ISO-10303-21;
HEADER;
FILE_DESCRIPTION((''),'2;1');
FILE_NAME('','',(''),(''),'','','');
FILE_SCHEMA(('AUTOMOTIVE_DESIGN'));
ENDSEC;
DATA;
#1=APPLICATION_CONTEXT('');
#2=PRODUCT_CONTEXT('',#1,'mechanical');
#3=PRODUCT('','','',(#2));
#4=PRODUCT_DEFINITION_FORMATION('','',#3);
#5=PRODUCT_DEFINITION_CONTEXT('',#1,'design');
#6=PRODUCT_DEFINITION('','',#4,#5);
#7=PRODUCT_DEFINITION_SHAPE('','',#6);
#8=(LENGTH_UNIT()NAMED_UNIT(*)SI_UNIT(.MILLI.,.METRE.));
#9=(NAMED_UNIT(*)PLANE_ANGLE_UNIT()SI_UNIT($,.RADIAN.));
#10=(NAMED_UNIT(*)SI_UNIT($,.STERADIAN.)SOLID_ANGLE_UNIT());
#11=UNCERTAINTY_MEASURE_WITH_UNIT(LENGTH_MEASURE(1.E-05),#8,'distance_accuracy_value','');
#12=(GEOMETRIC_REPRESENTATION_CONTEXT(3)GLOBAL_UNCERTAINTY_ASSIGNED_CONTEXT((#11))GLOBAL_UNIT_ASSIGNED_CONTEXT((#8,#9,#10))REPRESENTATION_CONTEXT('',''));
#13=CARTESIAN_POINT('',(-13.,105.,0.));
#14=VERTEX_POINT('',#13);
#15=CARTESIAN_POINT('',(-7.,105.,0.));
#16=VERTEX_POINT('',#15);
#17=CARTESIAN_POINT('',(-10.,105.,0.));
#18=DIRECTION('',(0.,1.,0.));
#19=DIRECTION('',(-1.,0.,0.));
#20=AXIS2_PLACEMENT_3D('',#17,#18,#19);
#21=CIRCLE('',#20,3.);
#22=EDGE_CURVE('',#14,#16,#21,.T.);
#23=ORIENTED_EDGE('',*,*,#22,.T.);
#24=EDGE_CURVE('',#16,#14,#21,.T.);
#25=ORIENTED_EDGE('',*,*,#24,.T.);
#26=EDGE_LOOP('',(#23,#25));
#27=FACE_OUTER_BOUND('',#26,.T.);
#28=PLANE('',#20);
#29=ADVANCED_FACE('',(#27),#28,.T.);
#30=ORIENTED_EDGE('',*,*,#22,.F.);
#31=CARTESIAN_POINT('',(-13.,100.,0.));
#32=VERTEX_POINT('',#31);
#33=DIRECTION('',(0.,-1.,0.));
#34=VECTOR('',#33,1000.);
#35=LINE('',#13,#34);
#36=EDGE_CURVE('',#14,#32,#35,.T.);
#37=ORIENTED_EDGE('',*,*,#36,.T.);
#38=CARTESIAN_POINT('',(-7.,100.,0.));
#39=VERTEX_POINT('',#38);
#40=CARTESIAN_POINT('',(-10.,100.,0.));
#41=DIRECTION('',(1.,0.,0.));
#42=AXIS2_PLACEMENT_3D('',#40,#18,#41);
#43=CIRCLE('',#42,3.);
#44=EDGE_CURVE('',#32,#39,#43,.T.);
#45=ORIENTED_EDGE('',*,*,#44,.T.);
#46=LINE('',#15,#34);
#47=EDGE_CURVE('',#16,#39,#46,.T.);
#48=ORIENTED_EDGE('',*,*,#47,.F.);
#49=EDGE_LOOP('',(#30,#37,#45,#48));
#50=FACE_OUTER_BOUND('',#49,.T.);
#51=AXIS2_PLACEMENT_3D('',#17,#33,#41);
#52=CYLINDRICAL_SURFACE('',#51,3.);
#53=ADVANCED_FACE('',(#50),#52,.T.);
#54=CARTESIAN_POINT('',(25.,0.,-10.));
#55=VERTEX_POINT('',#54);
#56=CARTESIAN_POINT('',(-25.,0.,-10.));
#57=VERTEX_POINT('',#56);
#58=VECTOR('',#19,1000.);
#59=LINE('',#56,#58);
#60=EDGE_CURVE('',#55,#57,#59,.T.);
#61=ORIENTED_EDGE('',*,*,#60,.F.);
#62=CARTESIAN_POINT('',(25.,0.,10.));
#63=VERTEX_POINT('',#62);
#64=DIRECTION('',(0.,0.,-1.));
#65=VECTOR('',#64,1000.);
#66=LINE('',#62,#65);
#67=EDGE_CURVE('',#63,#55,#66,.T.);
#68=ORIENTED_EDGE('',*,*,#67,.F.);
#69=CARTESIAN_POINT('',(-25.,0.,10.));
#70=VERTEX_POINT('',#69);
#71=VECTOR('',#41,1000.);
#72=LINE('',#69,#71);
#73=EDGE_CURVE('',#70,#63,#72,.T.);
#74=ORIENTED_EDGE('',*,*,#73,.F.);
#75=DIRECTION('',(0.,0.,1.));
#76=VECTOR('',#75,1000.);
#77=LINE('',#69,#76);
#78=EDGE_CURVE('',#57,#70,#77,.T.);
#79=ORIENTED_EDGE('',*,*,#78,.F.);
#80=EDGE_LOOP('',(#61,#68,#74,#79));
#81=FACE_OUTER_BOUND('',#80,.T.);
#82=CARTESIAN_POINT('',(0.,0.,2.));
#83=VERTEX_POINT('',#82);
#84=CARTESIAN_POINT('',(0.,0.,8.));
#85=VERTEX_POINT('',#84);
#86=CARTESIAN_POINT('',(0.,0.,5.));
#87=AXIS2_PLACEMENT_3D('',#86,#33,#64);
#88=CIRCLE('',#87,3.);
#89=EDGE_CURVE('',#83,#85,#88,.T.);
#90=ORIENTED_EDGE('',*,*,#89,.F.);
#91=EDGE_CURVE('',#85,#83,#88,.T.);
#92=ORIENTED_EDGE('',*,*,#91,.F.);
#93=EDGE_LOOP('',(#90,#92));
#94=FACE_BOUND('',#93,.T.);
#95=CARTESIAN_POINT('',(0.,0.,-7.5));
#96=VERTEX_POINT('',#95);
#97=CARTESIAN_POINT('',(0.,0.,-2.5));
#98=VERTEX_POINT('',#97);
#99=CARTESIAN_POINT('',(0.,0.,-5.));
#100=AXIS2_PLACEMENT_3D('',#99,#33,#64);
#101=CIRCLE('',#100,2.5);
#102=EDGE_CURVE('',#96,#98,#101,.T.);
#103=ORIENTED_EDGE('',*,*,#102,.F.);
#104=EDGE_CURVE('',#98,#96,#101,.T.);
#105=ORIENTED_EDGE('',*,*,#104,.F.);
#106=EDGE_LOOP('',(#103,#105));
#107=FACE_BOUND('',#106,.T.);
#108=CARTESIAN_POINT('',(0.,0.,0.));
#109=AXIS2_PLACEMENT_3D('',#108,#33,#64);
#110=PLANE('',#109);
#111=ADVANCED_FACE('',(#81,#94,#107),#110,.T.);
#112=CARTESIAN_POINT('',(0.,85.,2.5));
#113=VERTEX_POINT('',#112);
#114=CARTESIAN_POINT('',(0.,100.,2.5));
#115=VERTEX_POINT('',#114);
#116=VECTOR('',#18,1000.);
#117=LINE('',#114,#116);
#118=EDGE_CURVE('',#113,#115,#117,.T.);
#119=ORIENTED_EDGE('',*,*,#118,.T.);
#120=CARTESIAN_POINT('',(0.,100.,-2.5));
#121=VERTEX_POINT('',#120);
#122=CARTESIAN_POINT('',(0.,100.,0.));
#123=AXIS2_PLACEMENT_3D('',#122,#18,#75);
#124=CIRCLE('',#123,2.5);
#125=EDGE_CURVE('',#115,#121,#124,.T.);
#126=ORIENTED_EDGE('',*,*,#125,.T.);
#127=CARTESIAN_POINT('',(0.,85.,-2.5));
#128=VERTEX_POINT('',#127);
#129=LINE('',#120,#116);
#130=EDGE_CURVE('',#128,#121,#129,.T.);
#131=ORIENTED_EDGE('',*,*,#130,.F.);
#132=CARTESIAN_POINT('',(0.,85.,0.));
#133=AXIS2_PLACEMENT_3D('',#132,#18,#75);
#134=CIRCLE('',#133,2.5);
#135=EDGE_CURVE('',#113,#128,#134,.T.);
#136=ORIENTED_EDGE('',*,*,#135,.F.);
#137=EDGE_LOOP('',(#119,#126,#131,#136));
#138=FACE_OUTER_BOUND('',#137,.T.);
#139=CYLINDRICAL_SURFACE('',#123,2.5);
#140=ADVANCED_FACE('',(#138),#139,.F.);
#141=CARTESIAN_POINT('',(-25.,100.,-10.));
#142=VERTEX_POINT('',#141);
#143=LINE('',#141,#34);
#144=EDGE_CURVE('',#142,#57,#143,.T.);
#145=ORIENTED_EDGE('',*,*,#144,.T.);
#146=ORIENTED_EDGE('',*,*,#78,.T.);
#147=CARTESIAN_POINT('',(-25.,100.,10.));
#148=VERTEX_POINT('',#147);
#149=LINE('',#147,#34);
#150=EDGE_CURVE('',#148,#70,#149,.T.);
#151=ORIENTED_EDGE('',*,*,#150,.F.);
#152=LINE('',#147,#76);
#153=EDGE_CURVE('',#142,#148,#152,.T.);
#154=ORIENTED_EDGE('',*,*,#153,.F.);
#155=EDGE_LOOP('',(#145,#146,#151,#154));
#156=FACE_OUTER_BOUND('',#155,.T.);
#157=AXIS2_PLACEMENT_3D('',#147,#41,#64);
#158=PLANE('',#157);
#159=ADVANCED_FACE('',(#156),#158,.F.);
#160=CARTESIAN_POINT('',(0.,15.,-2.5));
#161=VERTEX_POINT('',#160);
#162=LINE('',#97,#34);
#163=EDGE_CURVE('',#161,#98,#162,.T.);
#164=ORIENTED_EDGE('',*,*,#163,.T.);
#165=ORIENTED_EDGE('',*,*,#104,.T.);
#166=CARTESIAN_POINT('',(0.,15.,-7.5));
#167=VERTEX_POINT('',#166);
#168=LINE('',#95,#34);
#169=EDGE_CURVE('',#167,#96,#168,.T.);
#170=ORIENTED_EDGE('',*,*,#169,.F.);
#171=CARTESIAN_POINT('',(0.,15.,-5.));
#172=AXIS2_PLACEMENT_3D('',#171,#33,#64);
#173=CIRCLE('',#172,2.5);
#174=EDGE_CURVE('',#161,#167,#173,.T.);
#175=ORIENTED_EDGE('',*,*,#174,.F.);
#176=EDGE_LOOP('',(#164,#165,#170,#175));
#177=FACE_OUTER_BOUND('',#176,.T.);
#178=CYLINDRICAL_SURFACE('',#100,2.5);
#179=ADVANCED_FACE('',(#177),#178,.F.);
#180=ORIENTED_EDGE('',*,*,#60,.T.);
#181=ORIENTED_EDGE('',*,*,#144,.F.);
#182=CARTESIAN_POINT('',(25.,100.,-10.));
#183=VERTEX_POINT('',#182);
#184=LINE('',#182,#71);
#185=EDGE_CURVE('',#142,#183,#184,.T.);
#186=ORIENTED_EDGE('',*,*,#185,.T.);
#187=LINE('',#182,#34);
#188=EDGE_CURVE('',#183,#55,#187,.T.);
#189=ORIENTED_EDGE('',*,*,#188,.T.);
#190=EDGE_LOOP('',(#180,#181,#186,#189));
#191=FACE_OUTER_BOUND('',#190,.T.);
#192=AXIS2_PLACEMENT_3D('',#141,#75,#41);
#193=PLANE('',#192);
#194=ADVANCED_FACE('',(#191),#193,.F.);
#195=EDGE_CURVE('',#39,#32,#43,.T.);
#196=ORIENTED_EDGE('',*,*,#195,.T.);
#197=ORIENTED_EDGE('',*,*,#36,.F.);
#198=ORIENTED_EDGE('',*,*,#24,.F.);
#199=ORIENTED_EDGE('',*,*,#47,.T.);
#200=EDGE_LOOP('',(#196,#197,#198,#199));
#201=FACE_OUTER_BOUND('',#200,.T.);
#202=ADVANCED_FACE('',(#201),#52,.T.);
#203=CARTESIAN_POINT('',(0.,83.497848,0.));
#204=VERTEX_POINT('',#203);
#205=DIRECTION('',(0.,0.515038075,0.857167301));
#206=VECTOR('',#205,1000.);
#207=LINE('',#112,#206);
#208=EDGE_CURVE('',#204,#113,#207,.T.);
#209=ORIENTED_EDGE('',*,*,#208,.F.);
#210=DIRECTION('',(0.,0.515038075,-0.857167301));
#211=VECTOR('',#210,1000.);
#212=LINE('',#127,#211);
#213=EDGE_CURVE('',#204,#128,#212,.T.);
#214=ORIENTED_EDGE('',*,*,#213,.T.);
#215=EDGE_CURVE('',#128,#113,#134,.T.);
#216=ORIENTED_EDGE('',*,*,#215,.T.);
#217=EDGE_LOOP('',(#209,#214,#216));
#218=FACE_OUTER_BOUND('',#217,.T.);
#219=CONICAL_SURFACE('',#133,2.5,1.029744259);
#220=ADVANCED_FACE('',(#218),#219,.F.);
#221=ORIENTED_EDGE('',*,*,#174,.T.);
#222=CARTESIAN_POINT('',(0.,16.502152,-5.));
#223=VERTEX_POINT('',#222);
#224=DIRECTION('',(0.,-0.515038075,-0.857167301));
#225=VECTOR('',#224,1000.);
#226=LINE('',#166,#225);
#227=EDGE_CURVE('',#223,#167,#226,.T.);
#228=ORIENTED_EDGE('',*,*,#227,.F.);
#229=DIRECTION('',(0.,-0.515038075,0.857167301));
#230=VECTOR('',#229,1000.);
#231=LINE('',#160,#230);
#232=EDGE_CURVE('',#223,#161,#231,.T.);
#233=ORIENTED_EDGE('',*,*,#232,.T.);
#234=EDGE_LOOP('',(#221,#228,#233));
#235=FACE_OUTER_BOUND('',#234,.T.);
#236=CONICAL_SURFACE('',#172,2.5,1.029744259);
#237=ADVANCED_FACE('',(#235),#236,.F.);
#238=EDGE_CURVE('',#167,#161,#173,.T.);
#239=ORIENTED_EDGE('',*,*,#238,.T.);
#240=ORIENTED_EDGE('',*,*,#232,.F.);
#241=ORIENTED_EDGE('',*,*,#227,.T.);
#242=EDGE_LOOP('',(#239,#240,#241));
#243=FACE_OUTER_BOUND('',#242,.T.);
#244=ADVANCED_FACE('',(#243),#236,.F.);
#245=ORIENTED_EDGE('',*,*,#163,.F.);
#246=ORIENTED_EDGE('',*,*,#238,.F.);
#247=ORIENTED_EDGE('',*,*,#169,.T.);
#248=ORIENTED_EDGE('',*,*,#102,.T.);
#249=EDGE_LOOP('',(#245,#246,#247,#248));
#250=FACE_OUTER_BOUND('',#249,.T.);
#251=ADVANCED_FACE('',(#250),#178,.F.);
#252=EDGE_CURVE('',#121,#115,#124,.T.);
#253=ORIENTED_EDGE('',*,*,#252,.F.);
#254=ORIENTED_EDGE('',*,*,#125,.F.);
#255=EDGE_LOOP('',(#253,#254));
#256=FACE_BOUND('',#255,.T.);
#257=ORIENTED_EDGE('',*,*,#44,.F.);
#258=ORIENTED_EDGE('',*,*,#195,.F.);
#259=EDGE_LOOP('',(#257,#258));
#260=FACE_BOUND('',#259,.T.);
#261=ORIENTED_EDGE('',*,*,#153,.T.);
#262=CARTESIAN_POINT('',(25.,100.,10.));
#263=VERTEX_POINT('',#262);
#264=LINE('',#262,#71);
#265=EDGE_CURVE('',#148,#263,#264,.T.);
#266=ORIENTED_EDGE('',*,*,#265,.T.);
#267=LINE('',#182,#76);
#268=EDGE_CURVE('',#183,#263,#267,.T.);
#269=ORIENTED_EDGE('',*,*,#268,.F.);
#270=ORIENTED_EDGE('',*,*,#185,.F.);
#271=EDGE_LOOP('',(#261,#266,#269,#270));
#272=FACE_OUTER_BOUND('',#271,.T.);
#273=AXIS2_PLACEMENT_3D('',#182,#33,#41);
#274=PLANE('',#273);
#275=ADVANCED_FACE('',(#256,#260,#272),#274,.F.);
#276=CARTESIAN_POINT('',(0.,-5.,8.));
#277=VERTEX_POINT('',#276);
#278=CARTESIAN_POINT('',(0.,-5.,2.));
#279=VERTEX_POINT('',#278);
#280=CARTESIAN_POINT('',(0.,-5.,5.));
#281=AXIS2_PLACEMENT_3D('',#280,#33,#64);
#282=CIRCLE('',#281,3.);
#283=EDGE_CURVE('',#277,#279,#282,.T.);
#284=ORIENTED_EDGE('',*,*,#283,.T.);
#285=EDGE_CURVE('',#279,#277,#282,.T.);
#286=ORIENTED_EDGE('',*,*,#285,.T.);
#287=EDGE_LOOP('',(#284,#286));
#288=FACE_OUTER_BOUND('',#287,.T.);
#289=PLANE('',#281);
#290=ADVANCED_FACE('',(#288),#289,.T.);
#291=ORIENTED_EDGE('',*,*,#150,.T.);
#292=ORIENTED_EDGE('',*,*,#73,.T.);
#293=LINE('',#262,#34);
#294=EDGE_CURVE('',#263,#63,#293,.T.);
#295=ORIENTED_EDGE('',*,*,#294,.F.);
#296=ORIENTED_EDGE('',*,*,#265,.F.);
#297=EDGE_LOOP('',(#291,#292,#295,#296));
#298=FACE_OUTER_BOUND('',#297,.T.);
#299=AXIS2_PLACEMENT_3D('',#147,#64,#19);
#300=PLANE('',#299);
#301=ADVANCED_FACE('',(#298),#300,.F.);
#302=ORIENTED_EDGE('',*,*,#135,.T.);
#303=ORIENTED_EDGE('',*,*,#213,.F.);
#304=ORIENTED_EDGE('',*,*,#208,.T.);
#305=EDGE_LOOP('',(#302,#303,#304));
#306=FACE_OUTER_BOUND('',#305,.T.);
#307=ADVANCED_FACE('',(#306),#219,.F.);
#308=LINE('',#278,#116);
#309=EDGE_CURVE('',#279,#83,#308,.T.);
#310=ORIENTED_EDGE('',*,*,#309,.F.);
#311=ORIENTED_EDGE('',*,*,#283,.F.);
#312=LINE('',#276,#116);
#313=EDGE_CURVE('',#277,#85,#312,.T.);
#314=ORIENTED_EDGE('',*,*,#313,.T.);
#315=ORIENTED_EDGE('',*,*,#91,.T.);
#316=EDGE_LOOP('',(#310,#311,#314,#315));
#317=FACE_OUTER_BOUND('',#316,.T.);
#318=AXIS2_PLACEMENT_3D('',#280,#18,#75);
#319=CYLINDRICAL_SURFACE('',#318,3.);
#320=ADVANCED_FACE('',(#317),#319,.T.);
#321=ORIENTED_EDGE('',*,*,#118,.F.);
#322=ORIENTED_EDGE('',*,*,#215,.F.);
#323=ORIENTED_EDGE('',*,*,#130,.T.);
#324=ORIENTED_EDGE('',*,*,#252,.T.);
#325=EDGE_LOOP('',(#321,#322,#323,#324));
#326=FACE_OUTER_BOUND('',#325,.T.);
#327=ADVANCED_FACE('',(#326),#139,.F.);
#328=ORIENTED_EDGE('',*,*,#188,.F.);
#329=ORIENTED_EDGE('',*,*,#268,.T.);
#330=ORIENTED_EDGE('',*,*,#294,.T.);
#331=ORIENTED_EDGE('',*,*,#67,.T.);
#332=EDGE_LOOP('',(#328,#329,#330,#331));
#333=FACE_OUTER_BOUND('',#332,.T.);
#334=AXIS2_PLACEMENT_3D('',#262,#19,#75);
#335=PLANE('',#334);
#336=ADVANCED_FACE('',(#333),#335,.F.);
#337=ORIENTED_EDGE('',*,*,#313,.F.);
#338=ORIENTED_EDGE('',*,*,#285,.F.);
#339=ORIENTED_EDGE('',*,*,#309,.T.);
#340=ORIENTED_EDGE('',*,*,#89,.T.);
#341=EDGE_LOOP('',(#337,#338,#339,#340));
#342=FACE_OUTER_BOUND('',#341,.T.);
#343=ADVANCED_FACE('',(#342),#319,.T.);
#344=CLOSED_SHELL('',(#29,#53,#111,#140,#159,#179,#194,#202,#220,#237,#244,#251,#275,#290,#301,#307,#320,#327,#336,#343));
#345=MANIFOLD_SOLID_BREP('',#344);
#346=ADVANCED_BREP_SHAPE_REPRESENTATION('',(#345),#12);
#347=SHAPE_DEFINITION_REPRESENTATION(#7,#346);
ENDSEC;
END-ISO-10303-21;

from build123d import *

# Parameters (mm, degrees)
SKETCH1_W             = 50
SKETCH1_H             = 20
BOSS_EXTRUDE1_DEPTH   = 100
SKETCH2_R             = 3
BOSS_EXTRUDE2_DEPTH   = 5
M6_TAPPED_HOLE1_D     = 5
M6_TAPPED_HOLE1_DEPTH = 15
M6_TAPPED_HOLE1_TIP   = 1.502151548
SKETCH5_W             = 20
SKETCH5_H             = 30
BOSS_EXTRUDE3_DEPTH   = 120
M3_TAPPED_HOLE1_D     = 2.5
M3_TAPPED_HOLE1_DEPTH = 7.5
M3_TAPPED_HOLE1_TIP   = 0.751075774
SKETCH8_W             = 147.482871738
SKETCH8_H             = 30
CUT_EXTRUDE1_DEPTH    = 163.249807396
SKETCH9_R             = 3
BOSS_EXTRUDE4_DEPTH   = 5
M6_TAPPED_HOLE2_D     = 5
M6_TAPPED_HOLE2_DEPTH = 15
M6_TAPPED_HOLE2_TIP   = 1.502151548


with BuildPart() as part:
    # Sketch1 → Boss-Extrude1 (new body)
    with BuildSketch(Plane(origin=(0, 0, 0), x_dir=(1, 0, 0), z_dir=(0, 1, 0))):
        Rectangle(SKETCH1_W, SKETCH1_H)
    extrude(amount=BOSS_EXTRUDE1_DEPTH)

    # Sketch2 → Boss-Extrude2 (add)
    with BuildSketch(Plane.XZ):
        with Locations(Location((0, 5, 0), (0, 0, 270))):
            Circle(SKETCH2_R)
    extrude(amount=BOSS_EXTRUDE2_DEPTH)

    # M6 Tapped Hole1
    with Locations(Plane(origin=(0, 0, 0), x_dir=(-1, 0, 0), z_dir=(0, -1, 0))):
        with Locations((0, 5)):
            Hole(M6_TAPPED_HOLE1_D / 2, depth=M6_TAPPED_HOLE1_DEPTH)
            with Locations((0, 0, -(M6_TAPPED_HOLE1_DEPTH + M6_TAPPED_HOLE1_TIP / 2))):  # 118° drill point
                Cone(0, M6_TAPPED_HOLE1_D / 2, M6_TAPPED_HOLE1_TIP, mode=Mode.SUBTRACT)

    # Sketch5 → Boss-Extrude3 (add)
    with BuildSketch(Plane(origin=(25, 0, 0), x_dir=(0, 0, -1), z_dir=(1, 0, 0))):
        with Locations((0, 115)):
            Rectangle(SKETCH5_W, SKETCH5_H)
    extrude(amount=-BOSS_EXTRUDE3_DEPTH)

    # M3 Tapped Hole1
    with Locations(Plane.XY.offset(10)):
        with Locations((-63.4, 108), (-59.4, 112), (-67.4, 105)):
            Hole(M3_TAPPED_HOLE1_D / 2, depth=M3_TAPPED_HOLE1_DEPTH)
            with Locations((0, 0, -(M3_TAPPED_HOLE1_DEPTH + M3_TAPPED_HOLE1_TIP / 2))):  # 118° drill point
                Cone(0, M3_TAPPED_HOLE1_D / 2, M3_TAPPED_HOLE1_TIP, mode=Mode.SUBTRACT)

    # Sketch8 → Cut-Extrude1 (cut, through all)
    with BuildSketch(Plane.XY.offset(10)):
        with Locations((-48.741435869, 115)):
            Rectangle(SKETCH8_W, SKETCH8_H)
    extrude(amount=-CUT_EXTRUDE1_DEPTH, mode=Mode.SUBTRACT)

    # Sketch9 → Boss-Extrude4 (add)
    with BuildSketch(Plane(origin=(0, 100, 0), x_dir=(1, 0, 0), z_dir=(0, 1, 0))):
        with Locations((-10, 0)):
            Circle(SKETCH9_R)
    extrude(amount=BOSS_EXTRUDE4_DEPTH)

    # M6 Tapped Hole2
    with Locations(Plane(origin=(0, 100, 0), x_dir=(1, 0, 0), z_dir=(0, 1, 0))):
        with Locations((0, 0)):
            Hole(M6_TAPPED_HOLE2_D / 2, depth=M6_TAPPED_HOLE2_DEPTH)
            with Locations((0, 0, -(M6_TAPPED_HOLE2_DEPTH + M6_TAPPED_HOLE2_TIP / 2))):  # 118° drill point
                Cone(0, M6_TAPPED_HOLE2_D / 2, M6_TAPPED_HOLE2_TIP, mode=Mode.SUBTRACT)


solid = part.part
